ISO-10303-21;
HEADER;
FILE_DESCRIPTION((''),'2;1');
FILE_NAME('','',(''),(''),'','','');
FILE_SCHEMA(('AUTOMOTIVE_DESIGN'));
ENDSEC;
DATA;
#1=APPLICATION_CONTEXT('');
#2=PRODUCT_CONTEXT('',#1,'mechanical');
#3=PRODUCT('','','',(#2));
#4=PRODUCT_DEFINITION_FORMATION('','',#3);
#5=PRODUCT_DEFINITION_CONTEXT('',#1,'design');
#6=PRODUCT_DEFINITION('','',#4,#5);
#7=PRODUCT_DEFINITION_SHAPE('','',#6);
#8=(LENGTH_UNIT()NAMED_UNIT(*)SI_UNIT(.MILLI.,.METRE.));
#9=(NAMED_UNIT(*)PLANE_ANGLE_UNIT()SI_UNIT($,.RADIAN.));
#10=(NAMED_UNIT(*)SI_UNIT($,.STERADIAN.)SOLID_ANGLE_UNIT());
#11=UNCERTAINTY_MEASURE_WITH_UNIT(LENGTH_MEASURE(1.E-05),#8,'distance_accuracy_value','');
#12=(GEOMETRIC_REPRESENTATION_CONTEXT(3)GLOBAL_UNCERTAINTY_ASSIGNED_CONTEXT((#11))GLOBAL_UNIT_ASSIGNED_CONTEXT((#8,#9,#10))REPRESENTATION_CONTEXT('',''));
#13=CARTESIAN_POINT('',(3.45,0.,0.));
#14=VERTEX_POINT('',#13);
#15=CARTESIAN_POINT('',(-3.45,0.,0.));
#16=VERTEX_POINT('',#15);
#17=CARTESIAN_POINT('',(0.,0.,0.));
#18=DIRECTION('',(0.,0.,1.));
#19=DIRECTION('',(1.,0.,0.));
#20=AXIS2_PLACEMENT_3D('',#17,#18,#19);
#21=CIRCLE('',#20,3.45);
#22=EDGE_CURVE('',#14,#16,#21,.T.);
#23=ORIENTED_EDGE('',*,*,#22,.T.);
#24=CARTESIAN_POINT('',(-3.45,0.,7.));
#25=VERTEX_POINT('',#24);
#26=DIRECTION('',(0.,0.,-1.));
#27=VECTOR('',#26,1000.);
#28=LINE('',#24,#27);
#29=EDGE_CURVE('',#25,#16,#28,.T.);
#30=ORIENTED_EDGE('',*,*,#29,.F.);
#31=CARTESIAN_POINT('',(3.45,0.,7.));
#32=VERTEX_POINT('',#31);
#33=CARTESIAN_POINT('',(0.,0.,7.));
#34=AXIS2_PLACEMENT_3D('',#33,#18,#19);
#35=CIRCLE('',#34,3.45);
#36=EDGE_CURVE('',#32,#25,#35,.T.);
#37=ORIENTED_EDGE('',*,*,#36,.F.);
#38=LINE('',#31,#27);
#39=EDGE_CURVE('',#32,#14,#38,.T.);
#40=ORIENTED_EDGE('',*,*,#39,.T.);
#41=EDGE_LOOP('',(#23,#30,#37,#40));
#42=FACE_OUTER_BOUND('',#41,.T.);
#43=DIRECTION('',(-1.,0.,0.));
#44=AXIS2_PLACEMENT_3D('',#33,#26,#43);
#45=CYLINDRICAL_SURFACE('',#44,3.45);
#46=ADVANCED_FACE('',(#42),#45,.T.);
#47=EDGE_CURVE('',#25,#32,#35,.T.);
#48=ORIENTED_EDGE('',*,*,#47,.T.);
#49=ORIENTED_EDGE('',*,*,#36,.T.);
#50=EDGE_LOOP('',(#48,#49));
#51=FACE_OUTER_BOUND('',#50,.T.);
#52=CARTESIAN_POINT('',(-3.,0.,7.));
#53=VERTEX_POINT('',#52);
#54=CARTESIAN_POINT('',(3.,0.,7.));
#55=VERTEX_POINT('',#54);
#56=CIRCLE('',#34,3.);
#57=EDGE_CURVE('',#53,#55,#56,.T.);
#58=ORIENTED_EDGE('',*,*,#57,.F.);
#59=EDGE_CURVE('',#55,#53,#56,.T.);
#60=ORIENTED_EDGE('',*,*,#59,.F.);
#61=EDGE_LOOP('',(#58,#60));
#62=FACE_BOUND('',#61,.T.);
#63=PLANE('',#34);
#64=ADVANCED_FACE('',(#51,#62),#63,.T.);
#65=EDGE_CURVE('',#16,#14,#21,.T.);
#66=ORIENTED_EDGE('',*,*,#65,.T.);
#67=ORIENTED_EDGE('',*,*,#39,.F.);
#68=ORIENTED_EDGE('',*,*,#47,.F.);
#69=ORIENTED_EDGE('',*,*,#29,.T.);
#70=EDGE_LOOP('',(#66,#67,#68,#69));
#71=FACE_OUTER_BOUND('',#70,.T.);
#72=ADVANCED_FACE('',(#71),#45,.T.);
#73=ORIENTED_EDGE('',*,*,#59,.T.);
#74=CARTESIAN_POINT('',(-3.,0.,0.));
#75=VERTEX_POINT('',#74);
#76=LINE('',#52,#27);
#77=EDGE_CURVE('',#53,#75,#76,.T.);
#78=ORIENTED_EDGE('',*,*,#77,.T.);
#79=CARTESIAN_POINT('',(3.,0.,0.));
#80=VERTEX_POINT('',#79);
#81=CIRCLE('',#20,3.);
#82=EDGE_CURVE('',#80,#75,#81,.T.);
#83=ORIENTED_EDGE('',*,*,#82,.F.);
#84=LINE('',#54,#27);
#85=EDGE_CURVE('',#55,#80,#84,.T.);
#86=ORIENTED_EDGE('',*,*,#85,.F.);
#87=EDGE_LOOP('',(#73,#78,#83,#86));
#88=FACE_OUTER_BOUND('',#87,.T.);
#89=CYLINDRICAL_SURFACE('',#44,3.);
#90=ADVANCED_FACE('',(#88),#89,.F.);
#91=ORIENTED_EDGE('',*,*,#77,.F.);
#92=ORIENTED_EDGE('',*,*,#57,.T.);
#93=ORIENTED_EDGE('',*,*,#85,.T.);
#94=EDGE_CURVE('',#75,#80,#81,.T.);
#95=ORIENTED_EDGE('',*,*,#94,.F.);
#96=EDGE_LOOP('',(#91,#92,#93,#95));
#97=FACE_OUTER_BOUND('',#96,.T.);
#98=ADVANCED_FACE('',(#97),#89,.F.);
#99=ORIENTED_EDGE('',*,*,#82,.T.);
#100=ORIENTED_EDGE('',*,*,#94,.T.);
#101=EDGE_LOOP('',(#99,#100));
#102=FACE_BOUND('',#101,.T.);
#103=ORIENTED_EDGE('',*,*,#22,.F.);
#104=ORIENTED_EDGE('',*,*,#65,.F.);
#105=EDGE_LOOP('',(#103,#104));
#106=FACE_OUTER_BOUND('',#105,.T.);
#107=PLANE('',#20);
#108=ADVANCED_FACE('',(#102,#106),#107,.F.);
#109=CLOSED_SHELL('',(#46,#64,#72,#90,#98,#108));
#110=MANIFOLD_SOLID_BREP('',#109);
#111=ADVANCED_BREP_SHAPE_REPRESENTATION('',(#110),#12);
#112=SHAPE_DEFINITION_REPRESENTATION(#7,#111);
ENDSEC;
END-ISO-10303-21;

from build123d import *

# Parameters (mm, degrees)
SKETCH1_R           = 3.45
SKETCH1_R_2         = 3
BOSS_EXTRUDE1_DEPTH = 7


with BuildPart() as part:
    # Sketch1 → Boss-Extrude1 (new body)
    with BuildSketch(Plane.XY):
        Circle(SKETCH1_R)
        Circle(SKETCH1_R_2, mode=Mode.SUBTRACT)
    extrude(amount=BOSS_EXTRUDE1_DEPTH)


solid = part.part
